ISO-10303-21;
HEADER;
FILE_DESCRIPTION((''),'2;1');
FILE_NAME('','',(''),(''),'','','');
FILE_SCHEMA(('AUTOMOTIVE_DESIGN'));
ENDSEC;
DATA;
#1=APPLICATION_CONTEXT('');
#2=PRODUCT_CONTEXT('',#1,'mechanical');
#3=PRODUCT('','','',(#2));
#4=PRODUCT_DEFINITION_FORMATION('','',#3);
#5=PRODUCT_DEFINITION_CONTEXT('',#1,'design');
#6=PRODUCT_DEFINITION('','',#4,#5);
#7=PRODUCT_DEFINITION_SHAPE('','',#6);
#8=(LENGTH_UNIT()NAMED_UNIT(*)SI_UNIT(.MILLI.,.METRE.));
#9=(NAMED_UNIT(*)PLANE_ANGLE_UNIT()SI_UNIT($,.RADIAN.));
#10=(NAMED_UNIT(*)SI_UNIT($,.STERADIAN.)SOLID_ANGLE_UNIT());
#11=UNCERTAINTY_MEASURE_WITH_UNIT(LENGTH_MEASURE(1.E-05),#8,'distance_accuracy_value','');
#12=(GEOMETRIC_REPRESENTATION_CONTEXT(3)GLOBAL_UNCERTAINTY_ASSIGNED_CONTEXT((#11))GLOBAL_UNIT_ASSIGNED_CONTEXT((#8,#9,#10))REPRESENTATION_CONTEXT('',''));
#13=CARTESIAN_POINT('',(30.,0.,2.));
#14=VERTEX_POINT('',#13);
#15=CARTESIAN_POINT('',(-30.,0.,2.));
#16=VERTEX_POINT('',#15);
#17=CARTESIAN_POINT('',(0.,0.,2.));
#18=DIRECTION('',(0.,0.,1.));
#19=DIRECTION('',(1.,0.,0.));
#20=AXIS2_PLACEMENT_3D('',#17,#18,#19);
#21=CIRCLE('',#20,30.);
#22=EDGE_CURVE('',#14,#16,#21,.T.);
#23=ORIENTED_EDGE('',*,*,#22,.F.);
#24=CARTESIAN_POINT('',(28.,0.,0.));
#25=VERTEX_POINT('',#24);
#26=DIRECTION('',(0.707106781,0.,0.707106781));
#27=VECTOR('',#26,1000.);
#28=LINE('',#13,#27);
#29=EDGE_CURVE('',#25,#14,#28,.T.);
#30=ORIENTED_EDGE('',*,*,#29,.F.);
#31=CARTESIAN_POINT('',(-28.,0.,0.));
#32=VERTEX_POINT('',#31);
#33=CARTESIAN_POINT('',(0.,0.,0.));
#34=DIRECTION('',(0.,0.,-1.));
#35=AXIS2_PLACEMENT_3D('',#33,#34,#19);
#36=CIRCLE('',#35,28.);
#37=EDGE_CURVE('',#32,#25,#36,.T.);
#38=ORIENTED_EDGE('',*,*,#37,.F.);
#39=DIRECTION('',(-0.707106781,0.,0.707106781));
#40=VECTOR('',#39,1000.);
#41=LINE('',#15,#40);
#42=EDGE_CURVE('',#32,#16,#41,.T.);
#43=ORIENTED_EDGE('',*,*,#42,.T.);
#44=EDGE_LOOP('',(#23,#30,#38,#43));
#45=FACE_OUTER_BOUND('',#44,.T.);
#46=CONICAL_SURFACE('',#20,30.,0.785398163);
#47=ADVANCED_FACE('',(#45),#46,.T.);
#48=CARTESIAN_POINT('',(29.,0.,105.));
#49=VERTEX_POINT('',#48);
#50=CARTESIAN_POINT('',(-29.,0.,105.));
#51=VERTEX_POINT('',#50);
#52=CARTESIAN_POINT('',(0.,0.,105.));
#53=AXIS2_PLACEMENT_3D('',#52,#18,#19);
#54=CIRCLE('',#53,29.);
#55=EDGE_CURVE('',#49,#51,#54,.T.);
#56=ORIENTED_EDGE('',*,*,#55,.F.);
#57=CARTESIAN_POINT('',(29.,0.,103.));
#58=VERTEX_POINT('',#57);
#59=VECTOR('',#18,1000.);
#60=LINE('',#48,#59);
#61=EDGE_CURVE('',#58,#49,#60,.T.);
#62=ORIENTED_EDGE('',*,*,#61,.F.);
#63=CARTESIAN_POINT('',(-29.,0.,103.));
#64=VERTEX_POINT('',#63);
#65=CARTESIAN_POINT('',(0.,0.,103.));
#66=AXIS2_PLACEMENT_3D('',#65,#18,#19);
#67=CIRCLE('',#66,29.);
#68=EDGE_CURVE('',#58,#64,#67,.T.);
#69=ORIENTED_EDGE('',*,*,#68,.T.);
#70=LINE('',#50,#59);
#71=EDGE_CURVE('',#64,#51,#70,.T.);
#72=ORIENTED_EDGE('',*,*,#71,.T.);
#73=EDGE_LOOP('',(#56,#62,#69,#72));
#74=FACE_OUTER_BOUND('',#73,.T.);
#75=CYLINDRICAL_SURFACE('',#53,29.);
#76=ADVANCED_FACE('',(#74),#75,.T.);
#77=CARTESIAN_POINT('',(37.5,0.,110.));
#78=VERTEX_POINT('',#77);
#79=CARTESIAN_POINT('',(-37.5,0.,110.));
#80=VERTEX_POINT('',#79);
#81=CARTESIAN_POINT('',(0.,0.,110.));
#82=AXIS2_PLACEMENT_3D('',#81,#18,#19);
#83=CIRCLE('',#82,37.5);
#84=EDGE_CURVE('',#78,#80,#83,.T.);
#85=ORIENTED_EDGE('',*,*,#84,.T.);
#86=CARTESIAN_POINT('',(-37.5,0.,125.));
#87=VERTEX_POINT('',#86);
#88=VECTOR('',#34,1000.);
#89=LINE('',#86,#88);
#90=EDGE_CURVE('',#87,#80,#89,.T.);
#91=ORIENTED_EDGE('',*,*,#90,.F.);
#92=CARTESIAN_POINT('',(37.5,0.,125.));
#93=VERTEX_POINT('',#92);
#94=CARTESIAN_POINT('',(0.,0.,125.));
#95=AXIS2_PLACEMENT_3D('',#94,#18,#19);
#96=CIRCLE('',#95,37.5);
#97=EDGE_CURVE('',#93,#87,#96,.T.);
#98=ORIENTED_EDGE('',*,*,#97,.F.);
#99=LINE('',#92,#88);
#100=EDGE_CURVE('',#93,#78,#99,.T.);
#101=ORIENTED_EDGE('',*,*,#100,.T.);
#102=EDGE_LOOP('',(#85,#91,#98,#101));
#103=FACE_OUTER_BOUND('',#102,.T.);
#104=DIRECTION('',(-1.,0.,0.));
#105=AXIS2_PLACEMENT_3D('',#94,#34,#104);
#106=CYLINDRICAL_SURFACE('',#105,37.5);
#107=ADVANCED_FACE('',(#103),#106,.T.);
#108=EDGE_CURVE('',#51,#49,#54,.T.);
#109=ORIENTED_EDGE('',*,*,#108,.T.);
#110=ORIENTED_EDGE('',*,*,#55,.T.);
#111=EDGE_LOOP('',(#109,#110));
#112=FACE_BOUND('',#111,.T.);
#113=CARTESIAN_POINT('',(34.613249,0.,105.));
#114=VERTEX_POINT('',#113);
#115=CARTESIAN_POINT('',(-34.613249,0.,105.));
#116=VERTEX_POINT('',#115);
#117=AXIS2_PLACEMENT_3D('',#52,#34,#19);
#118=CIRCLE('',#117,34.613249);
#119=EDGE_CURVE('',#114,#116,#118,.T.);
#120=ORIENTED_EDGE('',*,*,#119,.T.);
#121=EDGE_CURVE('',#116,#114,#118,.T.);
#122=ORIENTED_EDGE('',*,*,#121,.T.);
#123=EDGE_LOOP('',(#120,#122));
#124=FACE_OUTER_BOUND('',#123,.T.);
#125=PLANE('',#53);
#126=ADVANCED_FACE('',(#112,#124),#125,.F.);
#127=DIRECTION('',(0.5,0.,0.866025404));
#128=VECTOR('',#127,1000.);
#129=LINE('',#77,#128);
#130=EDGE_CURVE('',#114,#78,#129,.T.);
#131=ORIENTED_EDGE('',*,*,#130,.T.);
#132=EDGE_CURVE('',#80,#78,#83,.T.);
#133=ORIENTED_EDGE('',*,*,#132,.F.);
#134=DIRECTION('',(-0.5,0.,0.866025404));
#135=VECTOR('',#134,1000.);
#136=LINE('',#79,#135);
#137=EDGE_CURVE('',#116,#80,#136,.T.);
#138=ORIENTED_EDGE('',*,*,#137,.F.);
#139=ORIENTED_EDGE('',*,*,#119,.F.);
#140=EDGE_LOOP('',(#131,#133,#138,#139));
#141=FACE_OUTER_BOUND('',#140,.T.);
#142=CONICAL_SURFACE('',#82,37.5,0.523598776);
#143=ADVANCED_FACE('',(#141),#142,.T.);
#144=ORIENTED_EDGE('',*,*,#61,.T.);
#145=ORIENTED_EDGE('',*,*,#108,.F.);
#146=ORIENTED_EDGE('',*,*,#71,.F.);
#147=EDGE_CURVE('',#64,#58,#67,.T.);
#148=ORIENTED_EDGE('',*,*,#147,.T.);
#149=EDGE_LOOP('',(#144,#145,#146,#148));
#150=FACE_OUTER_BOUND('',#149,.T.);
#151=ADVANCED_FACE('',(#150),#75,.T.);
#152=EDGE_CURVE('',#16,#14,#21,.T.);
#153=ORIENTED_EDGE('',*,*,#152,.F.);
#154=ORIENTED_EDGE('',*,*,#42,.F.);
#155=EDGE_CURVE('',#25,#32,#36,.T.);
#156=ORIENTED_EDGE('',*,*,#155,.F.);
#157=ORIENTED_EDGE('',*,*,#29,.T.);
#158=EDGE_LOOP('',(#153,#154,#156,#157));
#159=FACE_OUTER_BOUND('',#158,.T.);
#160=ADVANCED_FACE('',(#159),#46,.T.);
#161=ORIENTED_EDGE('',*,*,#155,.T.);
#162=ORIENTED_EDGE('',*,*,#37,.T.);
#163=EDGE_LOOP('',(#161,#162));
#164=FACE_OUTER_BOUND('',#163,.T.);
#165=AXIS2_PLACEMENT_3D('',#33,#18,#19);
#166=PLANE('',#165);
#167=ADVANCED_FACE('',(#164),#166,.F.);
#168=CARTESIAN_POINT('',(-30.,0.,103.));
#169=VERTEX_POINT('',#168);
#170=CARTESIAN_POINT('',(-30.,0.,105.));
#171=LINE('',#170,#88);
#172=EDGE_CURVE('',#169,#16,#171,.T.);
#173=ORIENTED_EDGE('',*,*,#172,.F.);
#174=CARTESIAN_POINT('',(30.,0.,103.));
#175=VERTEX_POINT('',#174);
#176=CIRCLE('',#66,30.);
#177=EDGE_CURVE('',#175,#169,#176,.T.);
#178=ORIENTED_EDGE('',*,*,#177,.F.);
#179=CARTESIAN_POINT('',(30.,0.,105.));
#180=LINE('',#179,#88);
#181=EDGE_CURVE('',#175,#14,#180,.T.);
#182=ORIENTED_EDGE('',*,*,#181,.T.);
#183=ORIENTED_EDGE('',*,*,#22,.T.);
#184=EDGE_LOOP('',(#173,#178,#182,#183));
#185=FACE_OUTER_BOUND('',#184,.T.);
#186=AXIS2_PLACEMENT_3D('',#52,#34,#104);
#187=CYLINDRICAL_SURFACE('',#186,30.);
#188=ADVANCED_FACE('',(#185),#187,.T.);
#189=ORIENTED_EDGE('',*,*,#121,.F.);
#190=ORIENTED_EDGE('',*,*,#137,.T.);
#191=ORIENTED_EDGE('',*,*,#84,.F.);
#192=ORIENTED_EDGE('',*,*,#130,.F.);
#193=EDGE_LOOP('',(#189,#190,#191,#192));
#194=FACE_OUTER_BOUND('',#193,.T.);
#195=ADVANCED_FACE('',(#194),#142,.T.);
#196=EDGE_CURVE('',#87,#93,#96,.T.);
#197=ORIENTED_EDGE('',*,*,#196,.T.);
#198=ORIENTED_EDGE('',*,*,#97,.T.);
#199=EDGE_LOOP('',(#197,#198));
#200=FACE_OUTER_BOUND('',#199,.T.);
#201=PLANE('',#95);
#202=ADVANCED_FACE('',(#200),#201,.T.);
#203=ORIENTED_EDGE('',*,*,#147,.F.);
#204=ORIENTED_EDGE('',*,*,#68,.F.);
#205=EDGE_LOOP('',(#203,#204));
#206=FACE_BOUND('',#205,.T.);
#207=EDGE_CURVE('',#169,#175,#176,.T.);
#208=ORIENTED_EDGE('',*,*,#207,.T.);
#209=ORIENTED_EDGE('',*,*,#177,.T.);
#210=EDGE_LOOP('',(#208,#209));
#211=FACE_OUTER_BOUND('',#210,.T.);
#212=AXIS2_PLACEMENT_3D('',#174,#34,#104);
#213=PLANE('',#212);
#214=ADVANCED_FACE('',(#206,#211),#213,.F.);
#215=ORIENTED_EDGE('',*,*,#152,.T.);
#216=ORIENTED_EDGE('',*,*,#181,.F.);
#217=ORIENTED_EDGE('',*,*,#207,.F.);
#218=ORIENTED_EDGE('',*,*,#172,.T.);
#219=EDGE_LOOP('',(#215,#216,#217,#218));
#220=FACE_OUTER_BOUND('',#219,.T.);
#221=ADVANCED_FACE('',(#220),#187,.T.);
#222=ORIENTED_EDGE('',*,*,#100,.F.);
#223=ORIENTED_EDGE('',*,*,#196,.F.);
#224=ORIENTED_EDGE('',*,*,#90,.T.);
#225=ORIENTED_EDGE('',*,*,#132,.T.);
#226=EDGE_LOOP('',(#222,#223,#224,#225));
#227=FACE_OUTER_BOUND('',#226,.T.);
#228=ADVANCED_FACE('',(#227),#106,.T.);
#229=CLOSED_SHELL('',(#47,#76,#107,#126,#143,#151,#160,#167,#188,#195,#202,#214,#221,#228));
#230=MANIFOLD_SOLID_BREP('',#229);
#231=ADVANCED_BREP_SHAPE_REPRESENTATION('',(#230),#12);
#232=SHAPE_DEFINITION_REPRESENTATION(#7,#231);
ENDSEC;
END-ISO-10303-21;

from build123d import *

# Parameters (mm, degrees)
SKETCH_1_R      = 30
EXTRUDE_1_DEPTH = 105
SKETCH_2_R      = 37.5
EXTRUDE_2_DEPTH = 20
CHAMFER_2_SIZE  = 2
SKETCH_3_W      = 1
SKETCH_3_H      = 2
CHAMFER_3_SIZE  = 5
CHAMFER_3_SIZE2 = 2.886751346


with BuildPart() as part:
    # 草图1 → 凸台-拉伸1 (new body)
    with BuildSketch(Plane.XY):
        Circle(SKETCH_1_R)
    extrude(amount=EXTRUDE_1_DEPTH)

    # 草图2 → 凸台-拉伸2 (add)
    with BuildSketch(Plane.XY.offset(105)):
        Circle(SKETCH_2_R)
    extrude(amount=EXTRUDE_2_DEPTH)

    # 倒角2
    chamfer_2_edges = [part.edges().sort_by_distance(p)[0] for p in [
        (-30, 0, 0),
    ]]
    chamfer(chamfer_2_edges, length=CHAMFER_2_SIZE)

    # 草图3 → 切除-旋转1 (revolve, cut)
    with BuildSketch(Plane(origin=(0, 0, 0), x_dir=(1, 0, 0), z_dir=(0, 1, 0))):
        with Locations((29.5, -104)):
            Rectangle(SKETCH_3_W, SKETCH_3_H)
    revolve(axis=Axis((0, 0, 105), (0, 0, -1)), mode=Mode.SUBTRACT)

    # 倒角3
    chamfer_3_edges = [part.edges().sort_by_distance(p)[0] for p in [
        (-37.5, 0, 105),
    ]]
    chamfer_3_side = [part.faces().sort_by_distance(p)[0] for p in [
        (-37.5, 0, 115),
    ]]
    chamfer(chamfer_3_edges, length=CHAMFER_3_SIZE, length2=CHAMFER_3_SIZE2, reference=chamfer_3_side[0])


solid = part.part
